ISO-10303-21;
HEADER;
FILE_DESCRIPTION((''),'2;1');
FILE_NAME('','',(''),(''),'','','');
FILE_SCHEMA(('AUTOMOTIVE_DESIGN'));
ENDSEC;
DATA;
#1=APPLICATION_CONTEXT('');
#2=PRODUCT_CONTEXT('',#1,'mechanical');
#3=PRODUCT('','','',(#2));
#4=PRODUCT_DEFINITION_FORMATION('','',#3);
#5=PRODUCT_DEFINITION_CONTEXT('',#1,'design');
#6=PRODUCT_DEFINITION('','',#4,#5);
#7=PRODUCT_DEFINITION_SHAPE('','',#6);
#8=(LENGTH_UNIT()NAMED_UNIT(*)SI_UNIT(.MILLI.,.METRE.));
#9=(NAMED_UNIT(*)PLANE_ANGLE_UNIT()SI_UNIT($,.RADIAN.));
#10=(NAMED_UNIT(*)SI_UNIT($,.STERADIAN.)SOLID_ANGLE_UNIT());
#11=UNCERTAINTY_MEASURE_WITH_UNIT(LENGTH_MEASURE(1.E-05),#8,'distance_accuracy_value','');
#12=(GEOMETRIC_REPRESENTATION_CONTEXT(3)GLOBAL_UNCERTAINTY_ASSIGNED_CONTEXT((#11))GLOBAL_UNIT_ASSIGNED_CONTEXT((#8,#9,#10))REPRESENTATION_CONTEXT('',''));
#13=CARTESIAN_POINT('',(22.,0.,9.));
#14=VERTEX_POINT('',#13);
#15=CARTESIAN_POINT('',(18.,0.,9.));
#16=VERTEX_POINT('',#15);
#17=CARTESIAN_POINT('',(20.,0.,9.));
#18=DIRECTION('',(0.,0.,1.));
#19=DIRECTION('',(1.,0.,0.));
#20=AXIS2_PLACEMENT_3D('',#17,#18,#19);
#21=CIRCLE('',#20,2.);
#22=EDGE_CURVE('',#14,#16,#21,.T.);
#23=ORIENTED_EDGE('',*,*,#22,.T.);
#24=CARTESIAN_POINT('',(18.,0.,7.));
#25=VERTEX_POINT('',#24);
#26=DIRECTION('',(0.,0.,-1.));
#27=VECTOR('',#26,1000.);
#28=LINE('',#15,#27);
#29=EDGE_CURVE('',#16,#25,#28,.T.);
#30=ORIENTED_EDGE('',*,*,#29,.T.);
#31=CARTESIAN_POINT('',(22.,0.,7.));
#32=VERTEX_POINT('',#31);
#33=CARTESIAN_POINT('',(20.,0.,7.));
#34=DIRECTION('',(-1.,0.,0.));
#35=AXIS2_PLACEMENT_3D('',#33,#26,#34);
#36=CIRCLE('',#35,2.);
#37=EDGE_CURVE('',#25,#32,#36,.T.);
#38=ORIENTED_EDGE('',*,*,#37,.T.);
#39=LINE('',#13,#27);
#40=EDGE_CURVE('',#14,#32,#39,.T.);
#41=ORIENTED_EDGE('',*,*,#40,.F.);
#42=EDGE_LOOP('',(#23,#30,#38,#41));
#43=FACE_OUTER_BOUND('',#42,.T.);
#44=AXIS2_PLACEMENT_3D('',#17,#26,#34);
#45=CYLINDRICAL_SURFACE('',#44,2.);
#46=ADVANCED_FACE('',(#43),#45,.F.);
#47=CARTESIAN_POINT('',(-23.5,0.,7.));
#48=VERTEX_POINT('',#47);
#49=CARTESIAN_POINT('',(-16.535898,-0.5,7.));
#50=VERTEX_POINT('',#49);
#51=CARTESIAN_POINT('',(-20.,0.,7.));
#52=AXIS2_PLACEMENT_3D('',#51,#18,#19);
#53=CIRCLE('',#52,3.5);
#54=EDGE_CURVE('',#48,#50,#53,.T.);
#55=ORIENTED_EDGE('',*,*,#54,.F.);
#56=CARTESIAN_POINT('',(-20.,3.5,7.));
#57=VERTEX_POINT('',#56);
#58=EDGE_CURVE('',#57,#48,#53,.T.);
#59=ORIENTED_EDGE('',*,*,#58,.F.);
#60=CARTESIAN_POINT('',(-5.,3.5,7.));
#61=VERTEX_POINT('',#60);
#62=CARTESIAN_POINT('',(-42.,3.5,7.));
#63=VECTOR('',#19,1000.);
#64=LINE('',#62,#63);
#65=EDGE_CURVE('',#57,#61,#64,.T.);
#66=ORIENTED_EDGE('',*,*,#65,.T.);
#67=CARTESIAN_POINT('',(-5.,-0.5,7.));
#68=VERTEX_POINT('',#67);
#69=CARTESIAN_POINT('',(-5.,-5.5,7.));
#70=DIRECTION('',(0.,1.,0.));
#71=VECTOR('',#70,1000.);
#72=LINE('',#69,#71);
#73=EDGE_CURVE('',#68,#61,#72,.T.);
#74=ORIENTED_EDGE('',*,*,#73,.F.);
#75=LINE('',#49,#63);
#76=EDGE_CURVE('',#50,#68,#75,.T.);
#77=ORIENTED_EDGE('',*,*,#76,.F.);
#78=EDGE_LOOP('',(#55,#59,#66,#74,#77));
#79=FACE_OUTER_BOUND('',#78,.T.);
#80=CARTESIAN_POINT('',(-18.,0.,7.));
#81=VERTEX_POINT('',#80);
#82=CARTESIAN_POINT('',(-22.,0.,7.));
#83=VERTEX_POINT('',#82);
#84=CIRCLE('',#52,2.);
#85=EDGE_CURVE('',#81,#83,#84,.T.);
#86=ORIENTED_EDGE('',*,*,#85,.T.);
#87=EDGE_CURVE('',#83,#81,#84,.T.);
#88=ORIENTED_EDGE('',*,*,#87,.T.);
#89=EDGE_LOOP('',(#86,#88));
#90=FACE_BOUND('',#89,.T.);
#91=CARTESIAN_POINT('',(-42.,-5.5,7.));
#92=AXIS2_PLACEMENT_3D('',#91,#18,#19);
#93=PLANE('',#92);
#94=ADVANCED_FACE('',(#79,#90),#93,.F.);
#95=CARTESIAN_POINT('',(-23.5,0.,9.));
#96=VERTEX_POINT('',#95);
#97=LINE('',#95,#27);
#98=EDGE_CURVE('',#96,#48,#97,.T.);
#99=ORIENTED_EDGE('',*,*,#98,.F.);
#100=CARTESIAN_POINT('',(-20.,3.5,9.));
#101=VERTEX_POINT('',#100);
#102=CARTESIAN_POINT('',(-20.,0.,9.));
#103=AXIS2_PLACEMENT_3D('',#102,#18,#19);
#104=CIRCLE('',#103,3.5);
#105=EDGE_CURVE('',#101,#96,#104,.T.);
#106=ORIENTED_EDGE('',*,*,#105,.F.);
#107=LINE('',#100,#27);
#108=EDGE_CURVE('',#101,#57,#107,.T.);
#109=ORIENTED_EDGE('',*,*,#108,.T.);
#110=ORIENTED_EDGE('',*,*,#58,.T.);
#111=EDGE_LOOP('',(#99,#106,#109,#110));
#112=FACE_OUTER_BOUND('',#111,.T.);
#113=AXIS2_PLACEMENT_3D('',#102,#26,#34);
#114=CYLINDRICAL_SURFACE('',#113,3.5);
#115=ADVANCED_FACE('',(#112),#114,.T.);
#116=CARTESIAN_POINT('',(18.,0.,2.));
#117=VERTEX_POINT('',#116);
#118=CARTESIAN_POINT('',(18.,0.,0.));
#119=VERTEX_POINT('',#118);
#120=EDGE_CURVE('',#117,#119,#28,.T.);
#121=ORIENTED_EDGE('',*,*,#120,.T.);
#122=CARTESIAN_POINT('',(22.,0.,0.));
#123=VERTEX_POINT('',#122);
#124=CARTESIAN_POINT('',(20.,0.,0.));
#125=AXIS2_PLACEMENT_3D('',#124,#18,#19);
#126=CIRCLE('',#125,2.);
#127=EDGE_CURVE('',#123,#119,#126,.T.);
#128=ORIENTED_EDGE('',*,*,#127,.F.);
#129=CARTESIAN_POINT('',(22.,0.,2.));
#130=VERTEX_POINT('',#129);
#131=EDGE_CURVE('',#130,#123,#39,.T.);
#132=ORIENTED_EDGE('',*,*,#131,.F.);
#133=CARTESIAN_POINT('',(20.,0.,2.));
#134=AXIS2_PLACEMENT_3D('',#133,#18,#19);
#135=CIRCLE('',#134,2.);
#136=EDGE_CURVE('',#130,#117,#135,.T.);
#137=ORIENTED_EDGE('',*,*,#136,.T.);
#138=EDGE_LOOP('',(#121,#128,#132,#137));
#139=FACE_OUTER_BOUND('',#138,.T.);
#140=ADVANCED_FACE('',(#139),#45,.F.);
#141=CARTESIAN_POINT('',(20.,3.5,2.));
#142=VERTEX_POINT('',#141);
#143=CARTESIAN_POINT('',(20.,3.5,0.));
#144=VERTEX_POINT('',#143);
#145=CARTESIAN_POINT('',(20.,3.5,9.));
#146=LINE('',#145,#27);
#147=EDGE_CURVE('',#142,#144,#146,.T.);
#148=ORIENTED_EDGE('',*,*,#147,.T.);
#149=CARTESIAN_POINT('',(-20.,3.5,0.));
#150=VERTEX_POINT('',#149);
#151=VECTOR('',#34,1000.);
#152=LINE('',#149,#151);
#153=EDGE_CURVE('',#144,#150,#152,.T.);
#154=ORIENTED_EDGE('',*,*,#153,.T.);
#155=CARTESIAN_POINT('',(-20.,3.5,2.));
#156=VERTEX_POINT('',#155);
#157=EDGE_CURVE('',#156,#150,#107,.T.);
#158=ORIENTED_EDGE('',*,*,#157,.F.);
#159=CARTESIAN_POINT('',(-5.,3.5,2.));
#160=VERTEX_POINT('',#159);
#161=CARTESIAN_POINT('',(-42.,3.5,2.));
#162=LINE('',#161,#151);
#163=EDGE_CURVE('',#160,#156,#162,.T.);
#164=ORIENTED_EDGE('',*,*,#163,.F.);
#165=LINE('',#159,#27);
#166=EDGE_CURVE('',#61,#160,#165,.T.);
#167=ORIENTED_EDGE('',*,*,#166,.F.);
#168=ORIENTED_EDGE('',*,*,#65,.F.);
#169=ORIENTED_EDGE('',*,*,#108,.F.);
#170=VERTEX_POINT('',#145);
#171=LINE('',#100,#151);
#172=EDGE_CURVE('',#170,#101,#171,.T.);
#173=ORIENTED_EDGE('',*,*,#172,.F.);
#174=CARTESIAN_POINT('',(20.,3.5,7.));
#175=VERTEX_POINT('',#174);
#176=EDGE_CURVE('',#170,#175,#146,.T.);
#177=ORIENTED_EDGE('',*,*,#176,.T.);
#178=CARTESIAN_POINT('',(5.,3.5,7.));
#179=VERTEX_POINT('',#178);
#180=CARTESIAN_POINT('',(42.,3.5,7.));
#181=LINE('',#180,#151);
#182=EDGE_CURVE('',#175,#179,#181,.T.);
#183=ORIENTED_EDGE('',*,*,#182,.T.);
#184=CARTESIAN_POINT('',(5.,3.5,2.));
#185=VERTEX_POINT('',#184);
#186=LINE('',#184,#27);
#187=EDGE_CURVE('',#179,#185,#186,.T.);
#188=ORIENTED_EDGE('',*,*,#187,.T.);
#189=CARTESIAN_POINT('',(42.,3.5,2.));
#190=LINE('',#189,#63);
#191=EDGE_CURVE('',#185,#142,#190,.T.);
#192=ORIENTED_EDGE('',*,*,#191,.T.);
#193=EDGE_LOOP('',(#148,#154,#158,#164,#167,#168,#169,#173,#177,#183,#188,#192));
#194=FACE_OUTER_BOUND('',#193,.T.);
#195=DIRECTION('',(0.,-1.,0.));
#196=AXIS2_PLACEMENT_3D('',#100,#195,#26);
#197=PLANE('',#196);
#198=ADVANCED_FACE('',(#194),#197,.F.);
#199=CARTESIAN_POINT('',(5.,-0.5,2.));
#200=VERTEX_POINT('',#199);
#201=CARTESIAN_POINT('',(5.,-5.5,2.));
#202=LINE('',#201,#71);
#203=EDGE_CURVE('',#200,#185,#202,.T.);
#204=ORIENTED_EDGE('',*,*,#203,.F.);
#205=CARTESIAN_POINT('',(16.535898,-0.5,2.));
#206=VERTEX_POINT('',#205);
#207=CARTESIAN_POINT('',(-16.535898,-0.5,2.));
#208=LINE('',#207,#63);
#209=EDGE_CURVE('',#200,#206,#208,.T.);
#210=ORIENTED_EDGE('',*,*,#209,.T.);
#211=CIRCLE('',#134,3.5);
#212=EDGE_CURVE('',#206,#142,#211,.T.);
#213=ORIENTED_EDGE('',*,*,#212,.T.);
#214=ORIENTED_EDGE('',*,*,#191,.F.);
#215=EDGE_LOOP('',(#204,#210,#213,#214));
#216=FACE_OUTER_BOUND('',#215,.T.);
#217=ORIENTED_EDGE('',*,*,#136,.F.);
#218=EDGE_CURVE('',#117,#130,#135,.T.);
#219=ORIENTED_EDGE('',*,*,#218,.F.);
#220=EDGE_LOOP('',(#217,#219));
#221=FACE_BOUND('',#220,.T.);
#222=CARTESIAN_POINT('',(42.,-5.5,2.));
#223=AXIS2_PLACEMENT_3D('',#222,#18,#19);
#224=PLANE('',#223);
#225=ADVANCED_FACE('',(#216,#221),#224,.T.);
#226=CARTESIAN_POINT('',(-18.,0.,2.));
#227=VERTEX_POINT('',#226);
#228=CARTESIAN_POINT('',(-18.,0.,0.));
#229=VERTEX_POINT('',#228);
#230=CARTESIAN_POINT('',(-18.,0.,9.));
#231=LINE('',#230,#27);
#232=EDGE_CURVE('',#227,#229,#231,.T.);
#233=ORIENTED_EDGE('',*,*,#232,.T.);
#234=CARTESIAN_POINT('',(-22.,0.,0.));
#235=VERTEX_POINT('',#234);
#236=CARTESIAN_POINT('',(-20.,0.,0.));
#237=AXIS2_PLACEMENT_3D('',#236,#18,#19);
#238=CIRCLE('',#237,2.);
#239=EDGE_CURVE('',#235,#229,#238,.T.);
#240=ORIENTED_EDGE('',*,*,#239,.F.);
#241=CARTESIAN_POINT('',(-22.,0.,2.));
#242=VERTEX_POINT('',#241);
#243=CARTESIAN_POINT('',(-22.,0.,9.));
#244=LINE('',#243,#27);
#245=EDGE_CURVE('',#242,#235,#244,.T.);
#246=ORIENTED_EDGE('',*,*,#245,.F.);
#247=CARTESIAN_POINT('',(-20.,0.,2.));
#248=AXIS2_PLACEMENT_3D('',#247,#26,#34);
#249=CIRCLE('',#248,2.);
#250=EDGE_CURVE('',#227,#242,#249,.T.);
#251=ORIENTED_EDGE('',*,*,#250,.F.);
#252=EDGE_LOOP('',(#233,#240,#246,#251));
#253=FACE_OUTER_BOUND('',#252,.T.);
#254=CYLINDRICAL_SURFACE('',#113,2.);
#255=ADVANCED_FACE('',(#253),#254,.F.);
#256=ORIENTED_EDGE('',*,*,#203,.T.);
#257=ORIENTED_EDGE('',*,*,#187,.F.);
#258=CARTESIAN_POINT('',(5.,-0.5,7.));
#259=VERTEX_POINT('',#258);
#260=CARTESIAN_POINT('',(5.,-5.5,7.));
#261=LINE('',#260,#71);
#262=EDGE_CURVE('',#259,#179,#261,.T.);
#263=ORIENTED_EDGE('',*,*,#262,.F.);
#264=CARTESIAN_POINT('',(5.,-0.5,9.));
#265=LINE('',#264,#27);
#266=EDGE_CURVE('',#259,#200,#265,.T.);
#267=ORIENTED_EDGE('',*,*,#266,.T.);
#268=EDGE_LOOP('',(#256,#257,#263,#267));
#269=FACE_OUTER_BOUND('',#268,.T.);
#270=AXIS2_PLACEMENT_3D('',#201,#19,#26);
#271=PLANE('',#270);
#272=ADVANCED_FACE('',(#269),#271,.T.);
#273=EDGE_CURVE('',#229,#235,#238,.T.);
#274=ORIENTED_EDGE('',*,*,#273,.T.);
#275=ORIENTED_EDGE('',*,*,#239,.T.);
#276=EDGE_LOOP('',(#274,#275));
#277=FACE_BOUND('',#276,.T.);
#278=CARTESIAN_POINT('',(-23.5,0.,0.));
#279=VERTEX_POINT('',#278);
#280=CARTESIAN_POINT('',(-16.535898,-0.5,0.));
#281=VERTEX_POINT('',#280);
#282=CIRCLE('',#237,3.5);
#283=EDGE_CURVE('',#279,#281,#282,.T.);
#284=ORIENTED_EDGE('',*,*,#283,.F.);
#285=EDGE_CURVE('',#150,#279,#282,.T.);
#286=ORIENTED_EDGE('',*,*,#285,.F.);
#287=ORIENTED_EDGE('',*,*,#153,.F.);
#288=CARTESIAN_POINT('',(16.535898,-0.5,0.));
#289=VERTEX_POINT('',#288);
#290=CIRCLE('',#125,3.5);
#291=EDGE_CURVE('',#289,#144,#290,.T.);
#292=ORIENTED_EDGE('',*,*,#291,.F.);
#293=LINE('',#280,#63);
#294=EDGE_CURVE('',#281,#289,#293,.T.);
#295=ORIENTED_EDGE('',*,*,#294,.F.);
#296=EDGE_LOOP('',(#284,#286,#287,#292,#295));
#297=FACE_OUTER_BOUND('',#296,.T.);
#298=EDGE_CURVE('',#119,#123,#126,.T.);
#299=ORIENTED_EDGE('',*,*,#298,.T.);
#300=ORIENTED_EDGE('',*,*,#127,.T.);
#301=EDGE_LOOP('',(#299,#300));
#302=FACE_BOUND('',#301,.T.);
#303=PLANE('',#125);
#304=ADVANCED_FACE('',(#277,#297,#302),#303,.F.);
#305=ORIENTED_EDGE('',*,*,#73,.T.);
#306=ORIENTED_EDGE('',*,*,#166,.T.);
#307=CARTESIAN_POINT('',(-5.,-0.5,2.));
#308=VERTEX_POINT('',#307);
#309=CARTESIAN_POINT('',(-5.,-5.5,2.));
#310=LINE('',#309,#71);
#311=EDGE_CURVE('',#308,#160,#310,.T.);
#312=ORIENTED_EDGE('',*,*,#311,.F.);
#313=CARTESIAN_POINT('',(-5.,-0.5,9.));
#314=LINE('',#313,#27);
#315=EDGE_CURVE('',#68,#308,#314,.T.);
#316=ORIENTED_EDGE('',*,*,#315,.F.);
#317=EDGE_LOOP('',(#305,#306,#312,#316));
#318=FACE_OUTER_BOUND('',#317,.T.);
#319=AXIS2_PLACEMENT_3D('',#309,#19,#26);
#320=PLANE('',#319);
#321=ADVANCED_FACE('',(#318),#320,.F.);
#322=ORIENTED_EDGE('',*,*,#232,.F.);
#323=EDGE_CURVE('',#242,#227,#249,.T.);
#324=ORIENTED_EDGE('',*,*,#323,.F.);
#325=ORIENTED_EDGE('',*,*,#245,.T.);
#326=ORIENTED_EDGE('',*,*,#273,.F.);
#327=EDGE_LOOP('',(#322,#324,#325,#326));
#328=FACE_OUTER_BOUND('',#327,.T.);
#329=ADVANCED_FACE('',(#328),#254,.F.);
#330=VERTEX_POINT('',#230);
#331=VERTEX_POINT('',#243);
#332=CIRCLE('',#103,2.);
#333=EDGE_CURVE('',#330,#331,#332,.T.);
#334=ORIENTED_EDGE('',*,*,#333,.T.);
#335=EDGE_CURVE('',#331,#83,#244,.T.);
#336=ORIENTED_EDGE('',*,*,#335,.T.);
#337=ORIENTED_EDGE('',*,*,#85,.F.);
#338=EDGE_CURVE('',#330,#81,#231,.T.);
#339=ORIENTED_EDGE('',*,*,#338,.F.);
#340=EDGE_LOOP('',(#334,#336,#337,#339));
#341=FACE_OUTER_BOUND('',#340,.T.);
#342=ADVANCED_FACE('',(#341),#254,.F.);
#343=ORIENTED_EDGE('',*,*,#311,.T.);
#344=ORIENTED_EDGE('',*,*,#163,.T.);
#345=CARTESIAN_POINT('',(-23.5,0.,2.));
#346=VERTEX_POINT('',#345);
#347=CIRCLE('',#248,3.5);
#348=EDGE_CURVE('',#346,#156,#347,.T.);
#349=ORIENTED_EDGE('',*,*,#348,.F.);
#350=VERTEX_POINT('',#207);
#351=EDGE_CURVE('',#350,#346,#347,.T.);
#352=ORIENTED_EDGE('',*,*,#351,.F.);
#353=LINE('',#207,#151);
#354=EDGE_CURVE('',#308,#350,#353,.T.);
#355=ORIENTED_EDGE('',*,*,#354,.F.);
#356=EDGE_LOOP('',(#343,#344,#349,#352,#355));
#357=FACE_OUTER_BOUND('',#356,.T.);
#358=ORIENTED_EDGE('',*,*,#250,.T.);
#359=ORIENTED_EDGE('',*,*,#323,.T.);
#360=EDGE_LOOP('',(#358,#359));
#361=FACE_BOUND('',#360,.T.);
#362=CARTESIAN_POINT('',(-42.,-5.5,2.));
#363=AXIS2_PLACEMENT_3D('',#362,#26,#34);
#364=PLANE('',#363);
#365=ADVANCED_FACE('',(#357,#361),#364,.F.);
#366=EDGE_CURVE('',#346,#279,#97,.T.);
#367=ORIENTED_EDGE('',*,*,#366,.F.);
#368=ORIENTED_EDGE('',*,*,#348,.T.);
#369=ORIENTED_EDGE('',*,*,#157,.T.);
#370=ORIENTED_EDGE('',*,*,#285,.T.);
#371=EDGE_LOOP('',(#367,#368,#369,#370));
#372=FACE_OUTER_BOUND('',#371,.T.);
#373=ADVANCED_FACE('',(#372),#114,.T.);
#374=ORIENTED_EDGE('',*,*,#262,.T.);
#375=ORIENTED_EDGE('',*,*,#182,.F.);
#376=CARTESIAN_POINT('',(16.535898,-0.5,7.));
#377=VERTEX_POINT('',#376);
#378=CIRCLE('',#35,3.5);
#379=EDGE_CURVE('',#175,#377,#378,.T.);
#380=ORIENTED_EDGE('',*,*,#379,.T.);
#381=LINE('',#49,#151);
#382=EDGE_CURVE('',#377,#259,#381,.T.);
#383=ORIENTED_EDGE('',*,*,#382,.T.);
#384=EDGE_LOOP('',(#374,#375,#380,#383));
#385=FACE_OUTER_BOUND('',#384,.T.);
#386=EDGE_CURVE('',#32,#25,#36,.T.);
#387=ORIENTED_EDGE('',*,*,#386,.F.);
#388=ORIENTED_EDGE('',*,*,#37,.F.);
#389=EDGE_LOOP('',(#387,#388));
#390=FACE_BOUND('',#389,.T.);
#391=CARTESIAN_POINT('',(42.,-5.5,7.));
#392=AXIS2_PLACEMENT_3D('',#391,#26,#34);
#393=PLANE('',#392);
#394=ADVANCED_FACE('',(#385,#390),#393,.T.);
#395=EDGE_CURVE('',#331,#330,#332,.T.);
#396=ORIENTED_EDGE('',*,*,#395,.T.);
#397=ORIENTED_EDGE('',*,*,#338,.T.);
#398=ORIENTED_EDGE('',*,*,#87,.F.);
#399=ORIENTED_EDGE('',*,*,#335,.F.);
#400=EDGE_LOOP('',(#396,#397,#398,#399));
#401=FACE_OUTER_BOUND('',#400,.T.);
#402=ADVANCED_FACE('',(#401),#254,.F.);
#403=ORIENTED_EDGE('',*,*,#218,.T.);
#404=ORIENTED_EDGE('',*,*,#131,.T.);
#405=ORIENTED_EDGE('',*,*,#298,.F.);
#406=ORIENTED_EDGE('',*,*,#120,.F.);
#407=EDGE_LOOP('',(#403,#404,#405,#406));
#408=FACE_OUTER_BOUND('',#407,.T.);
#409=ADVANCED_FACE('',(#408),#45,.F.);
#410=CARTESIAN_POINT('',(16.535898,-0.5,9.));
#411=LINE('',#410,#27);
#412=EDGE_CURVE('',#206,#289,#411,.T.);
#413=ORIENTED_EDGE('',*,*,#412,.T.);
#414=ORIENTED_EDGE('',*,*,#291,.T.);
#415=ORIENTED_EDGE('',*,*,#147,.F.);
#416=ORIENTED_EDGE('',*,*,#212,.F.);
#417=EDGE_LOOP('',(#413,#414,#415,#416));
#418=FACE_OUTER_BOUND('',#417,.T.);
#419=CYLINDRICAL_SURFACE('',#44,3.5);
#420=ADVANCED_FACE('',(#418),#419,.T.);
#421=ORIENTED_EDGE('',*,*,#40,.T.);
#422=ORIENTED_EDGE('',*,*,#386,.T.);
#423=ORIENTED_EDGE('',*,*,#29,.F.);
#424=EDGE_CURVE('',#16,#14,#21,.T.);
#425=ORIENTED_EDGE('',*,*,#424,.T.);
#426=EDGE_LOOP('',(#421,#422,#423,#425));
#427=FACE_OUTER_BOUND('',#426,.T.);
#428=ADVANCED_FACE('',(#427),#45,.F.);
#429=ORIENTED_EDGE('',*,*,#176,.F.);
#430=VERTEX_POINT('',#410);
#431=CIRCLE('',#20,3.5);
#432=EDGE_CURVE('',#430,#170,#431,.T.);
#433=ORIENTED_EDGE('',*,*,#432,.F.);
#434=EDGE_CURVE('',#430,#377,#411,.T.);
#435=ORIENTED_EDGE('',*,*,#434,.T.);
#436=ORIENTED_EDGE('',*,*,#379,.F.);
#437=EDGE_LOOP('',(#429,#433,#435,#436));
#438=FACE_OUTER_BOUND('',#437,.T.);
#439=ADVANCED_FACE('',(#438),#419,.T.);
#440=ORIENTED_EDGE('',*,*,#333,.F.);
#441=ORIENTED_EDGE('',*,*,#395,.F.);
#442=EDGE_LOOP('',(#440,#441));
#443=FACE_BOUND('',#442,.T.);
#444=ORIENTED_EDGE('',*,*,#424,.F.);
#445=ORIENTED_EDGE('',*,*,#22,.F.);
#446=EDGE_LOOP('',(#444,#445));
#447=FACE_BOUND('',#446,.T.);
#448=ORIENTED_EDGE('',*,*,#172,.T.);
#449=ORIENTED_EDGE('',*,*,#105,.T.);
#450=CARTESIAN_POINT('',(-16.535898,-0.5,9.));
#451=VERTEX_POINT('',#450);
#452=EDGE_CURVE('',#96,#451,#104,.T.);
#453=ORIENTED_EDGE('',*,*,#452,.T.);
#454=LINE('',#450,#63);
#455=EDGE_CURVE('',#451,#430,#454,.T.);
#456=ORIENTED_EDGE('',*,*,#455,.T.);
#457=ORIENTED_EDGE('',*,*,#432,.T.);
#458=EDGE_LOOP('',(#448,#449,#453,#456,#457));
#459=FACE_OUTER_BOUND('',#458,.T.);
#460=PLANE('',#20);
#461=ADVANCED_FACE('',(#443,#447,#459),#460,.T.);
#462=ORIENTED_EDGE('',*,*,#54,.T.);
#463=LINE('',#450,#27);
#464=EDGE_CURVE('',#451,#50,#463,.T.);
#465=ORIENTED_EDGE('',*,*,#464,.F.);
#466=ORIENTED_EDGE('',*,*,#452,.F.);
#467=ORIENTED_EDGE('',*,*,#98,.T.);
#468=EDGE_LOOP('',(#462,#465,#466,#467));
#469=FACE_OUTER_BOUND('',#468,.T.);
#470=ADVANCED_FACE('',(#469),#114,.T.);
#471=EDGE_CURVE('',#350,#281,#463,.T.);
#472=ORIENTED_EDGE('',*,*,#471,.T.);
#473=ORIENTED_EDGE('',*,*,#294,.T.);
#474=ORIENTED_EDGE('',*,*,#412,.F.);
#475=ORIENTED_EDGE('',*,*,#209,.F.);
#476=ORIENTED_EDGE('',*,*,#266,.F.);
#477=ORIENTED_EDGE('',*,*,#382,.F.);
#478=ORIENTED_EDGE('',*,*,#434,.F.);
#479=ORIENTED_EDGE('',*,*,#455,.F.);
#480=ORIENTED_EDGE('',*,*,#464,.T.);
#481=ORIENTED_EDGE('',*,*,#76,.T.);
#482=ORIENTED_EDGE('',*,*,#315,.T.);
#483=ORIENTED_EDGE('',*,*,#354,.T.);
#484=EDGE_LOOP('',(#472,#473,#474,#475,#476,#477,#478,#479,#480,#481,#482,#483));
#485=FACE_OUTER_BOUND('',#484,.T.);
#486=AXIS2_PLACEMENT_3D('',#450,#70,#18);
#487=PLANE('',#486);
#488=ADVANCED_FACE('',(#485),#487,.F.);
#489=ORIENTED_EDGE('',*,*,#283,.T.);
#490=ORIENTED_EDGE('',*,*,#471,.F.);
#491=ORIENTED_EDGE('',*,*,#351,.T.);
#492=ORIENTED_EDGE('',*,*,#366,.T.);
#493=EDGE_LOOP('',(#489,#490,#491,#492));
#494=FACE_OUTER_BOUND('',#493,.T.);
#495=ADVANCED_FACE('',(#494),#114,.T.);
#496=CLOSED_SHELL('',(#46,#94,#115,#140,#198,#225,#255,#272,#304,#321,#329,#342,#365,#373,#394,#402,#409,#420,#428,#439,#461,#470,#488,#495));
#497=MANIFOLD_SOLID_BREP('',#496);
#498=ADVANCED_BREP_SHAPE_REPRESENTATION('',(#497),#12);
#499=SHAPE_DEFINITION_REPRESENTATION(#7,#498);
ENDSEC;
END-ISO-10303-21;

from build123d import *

# Parameters (mm, degrees)
SKETCH1_R           = 2
BOSS_EXTRUDE1_DEPTH = 9
SKETCH2_W           = 37
SKETCH2_H           = 5
CUT_EXTRUDE1_DEPTH  = 9


with BuildPart() as part:
    # Sketch1 → Boss-Extrude1 (new body)
    with BuildSketch(Plane.XY):
        with BuildLine():
            Line((-20, 3.5), (20, 3.5))
            ThreePointArc((20, 3.5), (22.645751311, -2.291287847), (16.535898385, -0.5))
            Line((16.535898385, -0.5), (-16.535898385, -0.5))
            ThreePointArc((-16.535898385, -0.5), (-22.645751311, -2.291287847), (-20, 3.5))
        make_face()
        with Locations((20, 0)):
            Circle(SKETCH1_R, mode=Mode.SUBTRACT)
        with Locations((-20, 0)):
            Circle(SKETCH1_R, mode=Mode.SUBTRACT)
    extrude(amount=BOSS_EXTRUDE1_DEPTH)

    # Sketch2 → Cut-Extrude1 (cut)
    with BuildSketch(Plane(origin=(0, 3.5, 0), x_dir=(1, 0, 0), z_dir=(0, 1, 0))):
        with Locations((-23.5, -4.5)):
            Rectangle(SKETCH2_W, SKETCH2_H)
    cut_extrude1 = extrude(amount=-CUT_EXTRUDE1_DEPTH, mode=Mode.SUBTRACT)

    # Mirror1: Cut-Extrude1 across plane
    add(cut_extrude1.mirror(Plane(origin=(0, 0, 0), x_dir=(0, 0, 1), z_dir=(1, 0, 0))), mode=Mode.SUBTRACT)


solid = part.part
